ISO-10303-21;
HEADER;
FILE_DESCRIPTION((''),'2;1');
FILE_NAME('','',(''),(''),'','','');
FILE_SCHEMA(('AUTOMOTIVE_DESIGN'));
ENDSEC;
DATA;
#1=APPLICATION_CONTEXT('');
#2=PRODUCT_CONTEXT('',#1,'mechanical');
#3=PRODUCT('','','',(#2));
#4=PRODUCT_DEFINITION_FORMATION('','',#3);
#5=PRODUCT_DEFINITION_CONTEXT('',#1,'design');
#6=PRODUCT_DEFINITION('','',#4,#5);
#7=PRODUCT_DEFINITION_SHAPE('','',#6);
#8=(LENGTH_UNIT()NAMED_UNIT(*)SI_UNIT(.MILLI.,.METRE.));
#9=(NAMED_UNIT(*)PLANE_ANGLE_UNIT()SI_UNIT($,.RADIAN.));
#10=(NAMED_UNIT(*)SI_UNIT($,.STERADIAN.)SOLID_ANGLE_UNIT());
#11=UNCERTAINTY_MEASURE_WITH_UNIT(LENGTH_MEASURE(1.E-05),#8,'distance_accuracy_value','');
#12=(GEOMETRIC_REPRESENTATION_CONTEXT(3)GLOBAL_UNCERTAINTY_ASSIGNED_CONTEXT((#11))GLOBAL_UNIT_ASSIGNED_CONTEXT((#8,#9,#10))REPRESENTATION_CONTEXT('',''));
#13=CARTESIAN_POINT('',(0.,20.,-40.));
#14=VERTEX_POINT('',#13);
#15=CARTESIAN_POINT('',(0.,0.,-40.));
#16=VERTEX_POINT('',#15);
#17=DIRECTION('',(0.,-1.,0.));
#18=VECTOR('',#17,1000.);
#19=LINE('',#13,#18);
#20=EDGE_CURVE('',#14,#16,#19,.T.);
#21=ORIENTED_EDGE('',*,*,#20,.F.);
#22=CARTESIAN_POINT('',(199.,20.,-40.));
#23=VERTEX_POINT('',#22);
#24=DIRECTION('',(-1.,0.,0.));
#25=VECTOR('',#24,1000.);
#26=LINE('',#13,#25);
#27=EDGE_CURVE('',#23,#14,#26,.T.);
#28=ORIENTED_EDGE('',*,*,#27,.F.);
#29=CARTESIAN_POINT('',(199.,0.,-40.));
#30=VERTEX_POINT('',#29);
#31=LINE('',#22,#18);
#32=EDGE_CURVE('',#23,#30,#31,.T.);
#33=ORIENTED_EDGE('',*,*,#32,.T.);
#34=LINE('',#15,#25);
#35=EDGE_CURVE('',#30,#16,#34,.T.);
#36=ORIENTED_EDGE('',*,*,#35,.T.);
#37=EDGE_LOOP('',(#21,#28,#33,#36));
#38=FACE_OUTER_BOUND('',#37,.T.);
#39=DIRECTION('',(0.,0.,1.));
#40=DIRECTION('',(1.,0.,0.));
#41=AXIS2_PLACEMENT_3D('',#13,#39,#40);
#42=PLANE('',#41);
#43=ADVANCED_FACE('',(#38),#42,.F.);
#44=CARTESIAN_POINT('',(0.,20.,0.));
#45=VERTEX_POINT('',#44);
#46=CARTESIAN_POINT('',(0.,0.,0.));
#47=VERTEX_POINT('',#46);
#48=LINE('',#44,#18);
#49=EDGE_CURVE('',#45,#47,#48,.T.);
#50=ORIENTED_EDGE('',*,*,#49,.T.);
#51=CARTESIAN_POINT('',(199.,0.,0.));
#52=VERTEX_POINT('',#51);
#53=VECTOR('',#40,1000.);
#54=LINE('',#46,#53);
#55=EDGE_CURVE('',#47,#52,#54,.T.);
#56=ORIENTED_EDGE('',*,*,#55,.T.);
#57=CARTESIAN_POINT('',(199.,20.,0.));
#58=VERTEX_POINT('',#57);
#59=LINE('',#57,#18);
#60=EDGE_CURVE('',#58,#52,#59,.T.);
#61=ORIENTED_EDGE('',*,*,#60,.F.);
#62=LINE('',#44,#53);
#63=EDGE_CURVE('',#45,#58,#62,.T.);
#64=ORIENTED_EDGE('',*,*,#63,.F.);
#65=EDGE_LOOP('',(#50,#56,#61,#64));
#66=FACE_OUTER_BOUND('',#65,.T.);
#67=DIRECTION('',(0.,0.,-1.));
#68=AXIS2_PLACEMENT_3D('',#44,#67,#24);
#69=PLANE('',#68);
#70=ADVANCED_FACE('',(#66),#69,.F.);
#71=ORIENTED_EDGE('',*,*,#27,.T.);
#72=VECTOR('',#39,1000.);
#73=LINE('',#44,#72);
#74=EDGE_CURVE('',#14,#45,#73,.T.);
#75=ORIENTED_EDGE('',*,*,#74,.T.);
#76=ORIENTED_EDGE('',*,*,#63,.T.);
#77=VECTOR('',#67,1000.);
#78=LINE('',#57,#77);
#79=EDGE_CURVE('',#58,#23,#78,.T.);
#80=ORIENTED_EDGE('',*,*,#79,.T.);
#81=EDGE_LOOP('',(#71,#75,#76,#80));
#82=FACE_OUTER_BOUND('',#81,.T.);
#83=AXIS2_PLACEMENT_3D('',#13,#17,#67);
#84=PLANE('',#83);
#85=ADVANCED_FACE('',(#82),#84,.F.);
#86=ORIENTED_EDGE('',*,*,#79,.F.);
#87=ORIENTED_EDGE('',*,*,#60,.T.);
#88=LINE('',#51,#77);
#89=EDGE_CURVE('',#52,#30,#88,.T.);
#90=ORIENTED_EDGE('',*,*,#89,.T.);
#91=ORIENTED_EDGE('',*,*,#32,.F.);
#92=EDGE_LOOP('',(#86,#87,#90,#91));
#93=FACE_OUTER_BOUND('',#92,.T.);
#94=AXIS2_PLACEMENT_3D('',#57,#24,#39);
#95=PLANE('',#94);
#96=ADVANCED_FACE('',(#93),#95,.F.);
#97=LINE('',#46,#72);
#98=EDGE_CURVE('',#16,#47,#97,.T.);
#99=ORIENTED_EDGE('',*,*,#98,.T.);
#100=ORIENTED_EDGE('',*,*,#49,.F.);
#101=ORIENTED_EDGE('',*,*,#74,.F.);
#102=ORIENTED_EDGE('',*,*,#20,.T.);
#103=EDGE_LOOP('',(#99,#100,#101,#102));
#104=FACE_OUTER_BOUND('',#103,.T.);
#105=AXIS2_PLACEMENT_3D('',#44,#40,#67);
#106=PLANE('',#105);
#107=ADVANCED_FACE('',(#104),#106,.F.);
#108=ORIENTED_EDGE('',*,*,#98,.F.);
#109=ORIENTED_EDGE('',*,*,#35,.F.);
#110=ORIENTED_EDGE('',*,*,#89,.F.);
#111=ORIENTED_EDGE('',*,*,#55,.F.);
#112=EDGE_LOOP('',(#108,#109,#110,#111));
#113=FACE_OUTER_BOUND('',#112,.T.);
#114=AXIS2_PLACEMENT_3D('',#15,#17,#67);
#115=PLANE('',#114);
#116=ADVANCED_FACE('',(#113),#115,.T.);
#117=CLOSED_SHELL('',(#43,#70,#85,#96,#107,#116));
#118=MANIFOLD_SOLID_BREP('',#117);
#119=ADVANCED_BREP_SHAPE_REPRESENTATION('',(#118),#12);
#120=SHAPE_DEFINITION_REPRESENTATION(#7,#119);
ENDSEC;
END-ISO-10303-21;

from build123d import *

# Parameters (mm, degrees)
SKETCH1_W           = 199
SKETCH1_H           = 40
BOSS_EXTRUDE1_DEPTH = 20


with BuildPart() as part:
    # Sketch1 → Boss-Extrude1 (new body)
    with BuildSketch(Plane(origin=(0, 0, 0), x_dir=(1, 0, 0), z_dir=(0, 1, 0))):
        with Locations((99.5, 20)):
            Rectangle(SKETCH1_W, SKETCH1_H)
    extrude(amount=BOSS_EXTRUDE1_DEPTH)


solid = part.part
